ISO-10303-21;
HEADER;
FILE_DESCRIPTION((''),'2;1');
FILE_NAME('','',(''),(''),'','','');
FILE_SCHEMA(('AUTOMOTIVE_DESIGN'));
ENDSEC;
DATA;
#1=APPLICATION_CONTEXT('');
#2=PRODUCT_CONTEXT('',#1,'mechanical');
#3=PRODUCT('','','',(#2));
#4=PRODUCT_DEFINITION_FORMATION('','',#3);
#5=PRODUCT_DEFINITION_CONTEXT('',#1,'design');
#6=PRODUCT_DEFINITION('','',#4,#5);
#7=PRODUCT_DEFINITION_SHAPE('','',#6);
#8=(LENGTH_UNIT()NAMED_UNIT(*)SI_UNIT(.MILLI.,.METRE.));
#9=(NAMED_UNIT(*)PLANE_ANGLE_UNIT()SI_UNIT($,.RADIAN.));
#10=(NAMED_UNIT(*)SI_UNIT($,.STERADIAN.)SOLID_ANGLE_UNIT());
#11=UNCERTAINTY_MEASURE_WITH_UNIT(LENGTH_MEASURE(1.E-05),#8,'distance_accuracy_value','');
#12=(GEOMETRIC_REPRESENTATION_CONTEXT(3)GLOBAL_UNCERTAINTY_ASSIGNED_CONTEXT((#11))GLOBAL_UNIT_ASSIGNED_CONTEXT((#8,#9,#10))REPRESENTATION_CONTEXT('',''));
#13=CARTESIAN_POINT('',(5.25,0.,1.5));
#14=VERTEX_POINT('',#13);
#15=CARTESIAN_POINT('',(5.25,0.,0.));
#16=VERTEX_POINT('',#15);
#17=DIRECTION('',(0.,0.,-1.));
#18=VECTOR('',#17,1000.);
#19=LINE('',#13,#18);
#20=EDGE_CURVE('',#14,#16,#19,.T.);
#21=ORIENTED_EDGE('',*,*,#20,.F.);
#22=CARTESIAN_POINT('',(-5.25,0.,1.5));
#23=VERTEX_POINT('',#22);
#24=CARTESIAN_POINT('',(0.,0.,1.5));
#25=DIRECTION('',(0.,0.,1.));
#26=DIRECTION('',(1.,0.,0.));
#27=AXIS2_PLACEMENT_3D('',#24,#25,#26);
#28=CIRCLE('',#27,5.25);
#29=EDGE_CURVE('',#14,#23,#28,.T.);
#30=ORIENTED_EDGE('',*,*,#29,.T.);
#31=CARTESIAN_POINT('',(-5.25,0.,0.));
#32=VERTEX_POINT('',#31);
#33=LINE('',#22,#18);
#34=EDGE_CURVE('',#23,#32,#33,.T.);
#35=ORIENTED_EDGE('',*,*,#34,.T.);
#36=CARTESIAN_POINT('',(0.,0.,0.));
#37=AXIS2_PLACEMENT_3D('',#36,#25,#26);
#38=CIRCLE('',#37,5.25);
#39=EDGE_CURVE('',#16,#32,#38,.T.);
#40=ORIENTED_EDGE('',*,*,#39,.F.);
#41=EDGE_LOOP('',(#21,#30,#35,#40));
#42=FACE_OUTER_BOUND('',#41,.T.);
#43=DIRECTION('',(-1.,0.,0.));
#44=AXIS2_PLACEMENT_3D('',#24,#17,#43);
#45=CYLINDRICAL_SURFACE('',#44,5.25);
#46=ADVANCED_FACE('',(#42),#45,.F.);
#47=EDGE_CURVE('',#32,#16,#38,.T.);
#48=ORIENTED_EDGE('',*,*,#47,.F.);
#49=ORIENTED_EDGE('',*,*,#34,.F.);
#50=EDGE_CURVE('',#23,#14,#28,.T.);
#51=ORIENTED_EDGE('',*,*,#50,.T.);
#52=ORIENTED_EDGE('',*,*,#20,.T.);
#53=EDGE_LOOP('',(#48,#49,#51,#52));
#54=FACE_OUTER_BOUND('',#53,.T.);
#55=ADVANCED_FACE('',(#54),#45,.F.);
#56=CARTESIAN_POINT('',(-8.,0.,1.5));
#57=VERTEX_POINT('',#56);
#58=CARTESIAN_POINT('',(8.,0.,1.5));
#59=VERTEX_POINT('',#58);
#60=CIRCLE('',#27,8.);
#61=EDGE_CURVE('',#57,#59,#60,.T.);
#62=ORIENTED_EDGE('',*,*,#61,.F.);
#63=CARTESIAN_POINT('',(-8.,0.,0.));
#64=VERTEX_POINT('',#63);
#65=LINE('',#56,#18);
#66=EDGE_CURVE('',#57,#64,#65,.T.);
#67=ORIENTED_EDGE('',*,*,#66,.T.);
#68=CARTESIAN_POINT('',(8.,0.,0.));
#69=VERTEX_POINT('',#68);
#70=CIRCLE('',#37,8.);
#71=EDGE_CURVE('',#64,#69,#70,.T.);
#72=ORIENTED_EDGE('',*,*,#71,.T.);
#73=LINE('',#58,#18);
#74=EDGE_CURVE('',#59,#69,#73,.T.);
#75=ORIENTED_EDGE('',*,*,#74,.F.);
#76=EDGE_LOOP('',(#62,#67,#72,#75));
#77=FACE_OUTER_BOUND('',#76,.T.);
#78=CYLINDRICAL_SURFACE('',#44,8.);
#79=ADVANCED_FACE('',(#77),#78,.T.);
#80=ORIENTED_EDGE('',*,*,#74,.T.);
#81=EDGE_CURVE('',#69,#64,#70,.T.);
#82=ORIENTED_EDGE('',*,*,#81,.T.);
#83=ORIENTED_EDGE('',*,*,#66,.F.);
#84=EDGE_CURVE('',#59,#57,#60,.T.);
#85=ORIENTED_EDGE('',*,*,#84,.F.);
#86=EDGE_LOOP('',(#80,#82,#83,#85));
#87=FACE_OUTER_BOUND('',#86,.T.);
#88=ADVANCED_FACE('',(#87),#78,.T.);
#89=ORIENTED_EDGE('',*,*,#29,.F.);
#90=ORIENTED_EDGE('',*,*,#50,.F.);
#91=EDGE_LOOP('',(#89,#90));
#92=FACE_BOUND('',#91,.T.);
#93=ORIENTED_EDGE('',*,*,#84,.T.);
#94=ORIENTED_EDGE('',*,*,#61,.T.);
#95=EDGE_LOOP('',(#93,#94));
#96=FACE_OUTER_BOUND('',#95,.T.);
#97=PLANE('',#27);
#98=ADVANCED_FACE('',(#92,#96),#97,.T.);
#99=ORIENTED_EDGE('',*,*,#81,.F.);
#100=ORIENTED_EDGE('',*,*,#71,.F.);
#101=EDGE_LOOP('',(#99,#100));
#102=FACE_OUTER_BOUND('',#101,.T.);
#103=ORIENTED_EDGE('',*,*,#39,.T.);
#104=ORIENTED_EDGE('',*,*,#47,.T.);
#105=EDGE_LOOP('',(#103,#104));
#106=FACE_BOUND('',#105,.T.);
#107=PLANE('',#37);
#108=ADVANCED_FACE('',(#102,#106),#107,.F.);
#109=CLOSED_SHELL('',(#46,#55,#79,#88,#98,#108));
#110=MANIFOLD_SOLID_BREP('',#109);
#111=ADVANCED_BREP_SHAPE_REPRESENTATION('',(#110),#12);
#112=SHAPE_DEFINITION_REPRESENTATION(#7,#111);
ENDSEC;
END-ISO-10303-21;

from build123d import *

# Parameters (mm, degrees)
SKETCH_246_R    = 8
SKETCH_246_R_2  = 5.25
EXTRUDE_1_DEPTH = 1.5


with BuildPart() as part:
    # Sketch 246 → 拉伸1 (new body)
    with BuildSketch(Plane.XY):
        Circle(SKETCH_246_R)
        Circle(SKETCH_246_R_2, mode=Mode.SUBTRACT)
    extrude(amount=EXTRUDE_1_DEPTH)


solid = part.part
